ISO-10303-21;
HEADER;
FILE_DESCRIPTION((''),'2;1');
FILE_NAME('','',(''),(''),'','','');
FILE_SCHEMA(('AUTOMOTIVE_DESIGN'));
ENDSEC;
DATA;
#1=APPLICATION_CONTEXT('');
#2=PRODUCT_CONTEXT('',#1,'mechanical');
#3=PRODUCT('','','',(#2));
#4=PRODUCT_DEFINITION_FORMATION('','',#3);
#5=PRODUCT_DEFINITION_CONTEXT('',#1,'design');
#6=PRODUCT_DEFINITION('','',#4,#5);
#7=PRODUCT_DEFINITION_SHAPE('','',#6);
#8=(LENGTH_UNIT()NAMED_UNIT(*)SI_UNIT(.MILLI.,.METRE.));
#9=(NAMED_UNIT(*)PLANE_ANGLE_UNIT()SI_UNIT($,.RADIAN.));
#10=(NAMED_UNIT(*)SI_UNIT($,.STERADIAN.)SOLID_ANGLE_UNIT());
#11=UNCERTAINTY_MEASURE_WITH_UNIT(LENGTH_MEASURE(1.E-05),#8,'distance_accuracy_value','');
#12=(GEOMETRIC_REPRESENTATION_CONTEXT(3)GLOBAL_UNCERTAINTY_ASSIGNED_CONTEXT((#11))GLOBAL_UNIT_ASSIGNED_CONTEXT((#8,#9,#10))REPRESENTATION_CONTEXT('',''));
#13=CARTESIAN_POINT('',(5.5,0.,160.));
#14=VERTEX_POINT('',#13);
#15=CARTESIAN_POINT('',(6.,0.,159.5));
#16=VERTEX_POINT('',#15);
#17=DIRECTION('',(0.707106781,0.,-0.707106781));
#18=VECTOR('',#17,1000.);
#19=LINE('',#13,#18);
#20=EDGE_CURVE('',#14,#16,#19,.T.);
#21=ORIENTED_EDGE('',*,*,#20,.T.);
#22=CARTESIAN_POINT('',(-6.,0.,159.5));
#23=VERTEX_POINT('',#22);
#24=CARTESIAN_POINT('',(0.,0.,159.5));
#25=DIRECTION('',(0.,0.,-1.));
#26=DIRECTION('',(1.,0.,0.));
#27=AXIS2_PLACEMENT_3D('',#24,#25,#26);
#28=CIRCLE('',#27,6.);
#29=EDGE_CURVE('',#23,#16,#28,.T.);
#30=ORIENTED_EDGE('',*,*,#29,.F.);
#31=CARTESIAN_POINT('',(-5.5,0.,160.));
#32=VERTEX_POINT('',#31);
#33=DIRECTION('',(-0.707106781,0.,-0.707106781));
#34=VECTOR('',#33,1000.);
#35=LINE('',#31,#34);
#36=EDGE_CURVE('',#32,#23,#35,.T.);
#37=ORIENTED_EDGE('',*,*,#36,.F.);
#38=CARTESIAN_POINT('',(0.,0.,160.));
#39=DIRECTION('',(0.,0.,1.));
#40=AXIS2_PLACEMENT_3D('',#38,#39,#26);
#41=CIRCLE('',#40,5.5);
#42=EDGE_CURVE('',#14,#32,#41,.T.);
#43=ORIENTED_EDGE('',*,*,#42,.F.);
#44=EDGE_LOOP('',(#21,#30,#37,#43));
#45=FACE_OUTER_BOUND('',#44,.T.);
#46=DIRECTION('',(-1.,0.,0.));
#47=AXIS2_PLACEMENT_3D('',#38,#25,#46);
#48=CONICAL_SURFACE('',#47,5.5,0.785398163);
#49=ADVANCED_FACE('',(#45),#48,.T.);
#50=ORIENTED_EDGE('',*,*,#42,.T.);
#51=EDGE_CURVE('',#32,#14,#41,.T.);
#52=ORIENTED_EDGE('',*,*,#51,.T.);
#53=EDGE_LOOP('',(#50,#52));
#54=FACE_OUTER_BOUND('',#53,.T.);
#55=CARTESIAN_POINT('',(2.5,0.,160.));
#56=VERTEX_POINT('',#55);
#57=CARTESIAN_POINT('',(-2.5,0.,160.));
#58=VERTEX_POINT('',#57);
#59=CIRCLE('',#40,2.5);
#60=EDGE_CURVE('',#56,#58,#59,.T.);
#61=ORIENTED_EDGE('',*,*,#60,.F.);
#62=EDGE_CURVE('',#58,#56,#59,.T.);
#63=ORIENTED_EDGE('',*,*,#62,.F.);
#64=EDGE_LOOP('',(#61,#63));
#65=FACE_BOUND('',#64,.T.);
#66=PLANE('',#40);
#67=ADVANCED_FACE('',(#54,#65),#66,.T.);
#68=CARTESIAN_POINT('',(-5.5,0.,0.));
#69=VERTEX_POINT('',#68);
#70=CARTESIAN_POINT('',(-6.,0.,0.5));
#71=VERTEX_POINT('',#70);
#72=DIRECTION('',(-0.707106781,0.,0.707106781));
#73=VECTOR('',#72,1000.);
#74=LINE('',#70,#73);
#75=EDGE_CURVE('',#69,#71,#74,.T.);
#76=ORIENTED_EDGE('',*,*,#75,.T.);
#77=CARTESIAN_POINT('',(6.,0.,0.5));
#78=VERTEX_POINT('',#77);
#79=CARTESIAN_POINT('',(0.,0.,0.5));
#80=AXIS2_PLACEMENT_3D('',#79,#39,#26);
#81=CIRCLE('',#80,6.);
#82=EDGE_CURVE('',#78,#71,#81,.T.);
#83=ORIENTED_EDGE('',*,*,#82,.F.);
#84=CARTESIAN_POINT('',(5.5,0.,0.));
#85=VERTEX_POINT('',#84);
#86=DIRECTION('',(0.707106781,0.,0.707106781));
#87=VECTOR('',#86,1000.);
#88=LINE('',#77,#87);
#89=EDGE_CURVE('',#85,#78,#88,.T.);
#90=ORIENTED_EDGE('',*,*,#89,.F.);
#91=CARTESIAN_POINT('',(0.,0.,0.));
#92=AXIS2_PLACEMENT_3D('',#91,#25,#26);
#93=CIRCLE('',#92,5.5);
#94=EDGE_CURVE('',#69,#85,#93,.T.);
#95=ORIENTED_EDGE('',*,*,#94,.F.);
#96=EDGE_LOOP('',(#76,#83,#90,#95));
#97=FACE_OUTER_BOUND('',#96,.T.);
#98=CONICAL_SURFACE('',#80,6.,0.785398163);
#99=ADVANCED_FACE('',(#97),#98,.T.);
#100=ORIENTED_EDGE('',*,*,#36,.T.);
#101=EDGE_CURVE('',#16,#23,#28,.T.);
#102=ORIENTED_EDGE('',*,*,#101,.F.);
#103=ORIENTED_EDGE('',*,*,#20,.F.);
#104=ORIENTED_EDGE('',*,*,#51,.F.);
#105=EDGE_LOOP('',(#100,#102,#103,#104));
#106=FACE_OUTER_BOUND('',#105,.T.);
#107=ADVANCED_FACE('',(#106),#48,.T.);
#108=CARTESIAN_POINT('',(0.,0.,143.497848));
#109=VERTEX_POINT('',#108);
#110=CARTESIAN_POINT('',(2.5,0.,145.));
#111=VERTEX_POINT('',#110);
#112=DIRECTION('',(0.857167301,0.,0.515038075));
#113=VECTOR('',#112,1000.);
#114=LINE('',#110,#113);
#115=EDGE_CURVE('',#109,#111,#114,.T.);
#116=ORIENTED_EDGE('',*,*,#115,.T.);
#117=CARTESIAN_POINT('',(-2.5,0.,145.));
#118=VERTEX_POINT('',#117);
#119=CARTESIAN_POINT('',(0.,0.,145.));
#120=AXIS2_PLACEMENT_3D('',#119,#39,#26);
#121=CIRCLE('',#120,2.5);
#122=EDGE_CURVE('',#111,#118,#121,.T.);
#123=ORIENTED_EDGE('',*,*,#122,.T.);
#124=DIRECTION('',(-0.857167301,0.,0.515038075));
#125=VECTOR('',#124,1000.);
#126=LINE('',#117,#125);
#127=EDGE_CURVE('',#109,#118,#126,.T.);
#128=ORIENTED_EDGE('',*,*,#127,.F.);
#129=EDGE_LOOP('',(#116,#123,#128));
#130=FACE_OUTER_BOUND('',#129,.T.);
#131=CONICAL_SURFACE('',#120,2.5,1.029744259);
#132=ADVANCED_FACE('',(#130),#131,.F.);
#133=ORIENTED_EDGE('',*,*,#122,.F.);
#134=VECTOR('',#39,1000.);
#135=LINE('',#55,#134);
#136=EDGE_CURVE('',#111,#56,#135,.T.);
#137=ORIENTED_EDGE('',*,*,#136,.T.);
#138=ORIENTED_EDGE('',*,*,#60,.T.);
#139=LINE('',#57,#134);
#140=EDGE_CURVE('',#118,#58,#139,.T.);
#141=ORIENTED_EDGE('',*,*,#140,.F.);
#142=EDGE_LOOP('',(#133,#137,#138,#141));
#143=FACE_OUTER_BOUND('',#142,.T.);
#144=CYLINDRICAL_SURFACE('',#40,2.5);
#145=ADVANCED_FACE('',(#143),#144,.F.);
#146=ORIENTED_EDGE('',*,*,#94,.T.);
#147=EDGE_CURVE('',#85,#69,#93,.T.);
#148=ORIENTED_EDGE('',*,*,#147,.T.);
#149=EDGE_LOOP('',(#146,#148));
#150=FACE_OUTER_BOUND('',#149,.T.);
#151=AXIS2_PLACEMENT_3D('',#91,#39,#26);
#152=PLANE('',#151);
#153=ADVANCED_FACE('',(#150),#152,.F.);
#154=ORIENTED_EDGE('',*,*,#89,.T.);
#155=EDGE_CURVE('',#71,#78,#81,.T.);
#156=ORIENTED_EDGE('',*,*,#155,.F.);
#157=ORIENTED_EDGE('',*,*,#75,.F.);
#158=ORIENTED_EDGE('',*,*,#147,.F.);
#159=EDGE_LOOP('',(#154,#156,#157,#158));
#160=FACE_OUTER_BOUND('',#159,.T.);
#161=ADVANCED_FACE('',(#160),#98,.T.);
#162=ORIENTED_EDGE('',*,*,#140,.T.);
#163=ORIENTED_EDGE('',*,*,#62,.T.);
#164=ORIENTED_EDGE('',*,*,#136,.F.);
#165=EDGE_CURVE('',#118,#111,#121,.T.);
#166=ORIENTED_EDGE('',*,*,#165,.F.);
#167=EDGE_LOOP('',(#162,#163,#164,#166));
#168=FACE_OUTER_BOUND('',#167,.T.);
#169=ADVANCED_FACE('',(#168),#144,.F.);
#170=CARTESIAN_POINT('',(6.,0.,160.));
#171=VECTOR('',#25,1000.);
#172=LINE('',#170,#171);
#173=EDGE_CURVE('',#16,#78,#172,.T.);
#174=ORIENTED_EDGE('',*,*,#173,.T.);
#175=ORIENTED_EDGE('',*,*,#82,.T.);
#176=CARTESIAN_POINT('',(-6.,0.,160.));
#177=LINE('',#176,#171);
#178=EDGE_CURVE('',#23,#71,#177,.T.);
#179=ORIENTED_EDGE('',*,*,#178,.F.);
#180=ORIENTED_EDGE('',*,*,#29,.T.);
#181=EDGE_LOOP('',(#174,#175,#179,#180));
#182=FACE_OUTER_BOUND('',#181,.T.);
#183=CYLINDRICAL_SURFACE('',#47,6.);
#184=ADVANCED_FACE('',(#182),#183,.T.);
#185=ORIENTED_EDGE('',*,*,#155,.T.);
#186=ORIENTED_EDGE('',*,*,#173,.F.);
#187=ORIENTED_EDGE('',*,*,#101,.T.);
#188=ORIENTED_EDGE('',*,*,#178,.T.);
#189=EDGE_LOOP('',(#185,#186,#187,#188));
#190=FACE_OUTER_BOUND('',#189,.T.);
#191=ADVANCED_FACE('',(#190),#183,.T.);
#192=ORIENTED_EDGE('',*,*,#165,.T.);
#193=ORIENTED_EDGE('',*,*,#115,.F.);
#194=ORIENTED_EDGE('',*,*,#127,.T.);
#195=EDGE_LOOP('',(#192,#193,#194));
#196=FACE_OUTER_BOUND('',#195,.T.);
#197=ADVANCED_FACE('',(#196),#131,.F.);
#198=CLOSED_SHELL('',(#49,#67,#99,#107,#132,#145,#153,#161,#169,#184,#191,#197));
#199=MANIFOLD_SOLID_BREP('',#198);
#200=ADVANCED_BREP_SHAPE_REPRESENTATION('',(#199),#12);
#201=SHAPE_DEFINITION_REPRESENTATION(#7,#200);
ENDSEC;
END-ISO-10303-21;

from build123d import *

# Parameters (mm, degrees)
SKETCH1_R             = 6
BOSS_EXTRUDE1_DEPTH   = 160
M6_TAPPED_HOLE1_D     = 5
M6_TAPPED_HOLE1_DEPTH = 15
M6_TAPPED_HOLE1_TIP   = 1.502151548
CHAMFER1_SIZE         = 0.5


with BuildPart() as part:
    # Sketch1 → Boss-Extrude1 (new body)
    with BuildSketch(Plane.XY):
        Circle(SKETCH1_R)
    extrude(amount=BOSS_EXTRUDE1_DEPTH)

    # M6 Tapped Hole1
    with Locations(Plane.XY.offset(160)):
        with Locations((0, 0)):
            Hole(M6_TAPPED_HOLE1_D / 2, depth=M6_TAPPED_HOLE1_DEPTH)
            with Locations((0, 0, -(M6_TAPPED_HOLE1_DEPTH + M6_TAPPED_HOLE1_TIP / 2))):  # 118° drill point
                Cone(0, M6_TAPPED_HOLE1_D / 2, M6_TAPPED_HOLE1_TIP, mode=Mode.SUBTRACT)

    # Chamfer1
    chamfer1_edges = [part.edges().sort_by_distance(p)[0] for p in [
        (-6, 0, 0),
        (-6, 0, 160),
    ]]
    chamfer(chamfer1_edges, length=CHAMFER1_SIZE)


solid = part.part
